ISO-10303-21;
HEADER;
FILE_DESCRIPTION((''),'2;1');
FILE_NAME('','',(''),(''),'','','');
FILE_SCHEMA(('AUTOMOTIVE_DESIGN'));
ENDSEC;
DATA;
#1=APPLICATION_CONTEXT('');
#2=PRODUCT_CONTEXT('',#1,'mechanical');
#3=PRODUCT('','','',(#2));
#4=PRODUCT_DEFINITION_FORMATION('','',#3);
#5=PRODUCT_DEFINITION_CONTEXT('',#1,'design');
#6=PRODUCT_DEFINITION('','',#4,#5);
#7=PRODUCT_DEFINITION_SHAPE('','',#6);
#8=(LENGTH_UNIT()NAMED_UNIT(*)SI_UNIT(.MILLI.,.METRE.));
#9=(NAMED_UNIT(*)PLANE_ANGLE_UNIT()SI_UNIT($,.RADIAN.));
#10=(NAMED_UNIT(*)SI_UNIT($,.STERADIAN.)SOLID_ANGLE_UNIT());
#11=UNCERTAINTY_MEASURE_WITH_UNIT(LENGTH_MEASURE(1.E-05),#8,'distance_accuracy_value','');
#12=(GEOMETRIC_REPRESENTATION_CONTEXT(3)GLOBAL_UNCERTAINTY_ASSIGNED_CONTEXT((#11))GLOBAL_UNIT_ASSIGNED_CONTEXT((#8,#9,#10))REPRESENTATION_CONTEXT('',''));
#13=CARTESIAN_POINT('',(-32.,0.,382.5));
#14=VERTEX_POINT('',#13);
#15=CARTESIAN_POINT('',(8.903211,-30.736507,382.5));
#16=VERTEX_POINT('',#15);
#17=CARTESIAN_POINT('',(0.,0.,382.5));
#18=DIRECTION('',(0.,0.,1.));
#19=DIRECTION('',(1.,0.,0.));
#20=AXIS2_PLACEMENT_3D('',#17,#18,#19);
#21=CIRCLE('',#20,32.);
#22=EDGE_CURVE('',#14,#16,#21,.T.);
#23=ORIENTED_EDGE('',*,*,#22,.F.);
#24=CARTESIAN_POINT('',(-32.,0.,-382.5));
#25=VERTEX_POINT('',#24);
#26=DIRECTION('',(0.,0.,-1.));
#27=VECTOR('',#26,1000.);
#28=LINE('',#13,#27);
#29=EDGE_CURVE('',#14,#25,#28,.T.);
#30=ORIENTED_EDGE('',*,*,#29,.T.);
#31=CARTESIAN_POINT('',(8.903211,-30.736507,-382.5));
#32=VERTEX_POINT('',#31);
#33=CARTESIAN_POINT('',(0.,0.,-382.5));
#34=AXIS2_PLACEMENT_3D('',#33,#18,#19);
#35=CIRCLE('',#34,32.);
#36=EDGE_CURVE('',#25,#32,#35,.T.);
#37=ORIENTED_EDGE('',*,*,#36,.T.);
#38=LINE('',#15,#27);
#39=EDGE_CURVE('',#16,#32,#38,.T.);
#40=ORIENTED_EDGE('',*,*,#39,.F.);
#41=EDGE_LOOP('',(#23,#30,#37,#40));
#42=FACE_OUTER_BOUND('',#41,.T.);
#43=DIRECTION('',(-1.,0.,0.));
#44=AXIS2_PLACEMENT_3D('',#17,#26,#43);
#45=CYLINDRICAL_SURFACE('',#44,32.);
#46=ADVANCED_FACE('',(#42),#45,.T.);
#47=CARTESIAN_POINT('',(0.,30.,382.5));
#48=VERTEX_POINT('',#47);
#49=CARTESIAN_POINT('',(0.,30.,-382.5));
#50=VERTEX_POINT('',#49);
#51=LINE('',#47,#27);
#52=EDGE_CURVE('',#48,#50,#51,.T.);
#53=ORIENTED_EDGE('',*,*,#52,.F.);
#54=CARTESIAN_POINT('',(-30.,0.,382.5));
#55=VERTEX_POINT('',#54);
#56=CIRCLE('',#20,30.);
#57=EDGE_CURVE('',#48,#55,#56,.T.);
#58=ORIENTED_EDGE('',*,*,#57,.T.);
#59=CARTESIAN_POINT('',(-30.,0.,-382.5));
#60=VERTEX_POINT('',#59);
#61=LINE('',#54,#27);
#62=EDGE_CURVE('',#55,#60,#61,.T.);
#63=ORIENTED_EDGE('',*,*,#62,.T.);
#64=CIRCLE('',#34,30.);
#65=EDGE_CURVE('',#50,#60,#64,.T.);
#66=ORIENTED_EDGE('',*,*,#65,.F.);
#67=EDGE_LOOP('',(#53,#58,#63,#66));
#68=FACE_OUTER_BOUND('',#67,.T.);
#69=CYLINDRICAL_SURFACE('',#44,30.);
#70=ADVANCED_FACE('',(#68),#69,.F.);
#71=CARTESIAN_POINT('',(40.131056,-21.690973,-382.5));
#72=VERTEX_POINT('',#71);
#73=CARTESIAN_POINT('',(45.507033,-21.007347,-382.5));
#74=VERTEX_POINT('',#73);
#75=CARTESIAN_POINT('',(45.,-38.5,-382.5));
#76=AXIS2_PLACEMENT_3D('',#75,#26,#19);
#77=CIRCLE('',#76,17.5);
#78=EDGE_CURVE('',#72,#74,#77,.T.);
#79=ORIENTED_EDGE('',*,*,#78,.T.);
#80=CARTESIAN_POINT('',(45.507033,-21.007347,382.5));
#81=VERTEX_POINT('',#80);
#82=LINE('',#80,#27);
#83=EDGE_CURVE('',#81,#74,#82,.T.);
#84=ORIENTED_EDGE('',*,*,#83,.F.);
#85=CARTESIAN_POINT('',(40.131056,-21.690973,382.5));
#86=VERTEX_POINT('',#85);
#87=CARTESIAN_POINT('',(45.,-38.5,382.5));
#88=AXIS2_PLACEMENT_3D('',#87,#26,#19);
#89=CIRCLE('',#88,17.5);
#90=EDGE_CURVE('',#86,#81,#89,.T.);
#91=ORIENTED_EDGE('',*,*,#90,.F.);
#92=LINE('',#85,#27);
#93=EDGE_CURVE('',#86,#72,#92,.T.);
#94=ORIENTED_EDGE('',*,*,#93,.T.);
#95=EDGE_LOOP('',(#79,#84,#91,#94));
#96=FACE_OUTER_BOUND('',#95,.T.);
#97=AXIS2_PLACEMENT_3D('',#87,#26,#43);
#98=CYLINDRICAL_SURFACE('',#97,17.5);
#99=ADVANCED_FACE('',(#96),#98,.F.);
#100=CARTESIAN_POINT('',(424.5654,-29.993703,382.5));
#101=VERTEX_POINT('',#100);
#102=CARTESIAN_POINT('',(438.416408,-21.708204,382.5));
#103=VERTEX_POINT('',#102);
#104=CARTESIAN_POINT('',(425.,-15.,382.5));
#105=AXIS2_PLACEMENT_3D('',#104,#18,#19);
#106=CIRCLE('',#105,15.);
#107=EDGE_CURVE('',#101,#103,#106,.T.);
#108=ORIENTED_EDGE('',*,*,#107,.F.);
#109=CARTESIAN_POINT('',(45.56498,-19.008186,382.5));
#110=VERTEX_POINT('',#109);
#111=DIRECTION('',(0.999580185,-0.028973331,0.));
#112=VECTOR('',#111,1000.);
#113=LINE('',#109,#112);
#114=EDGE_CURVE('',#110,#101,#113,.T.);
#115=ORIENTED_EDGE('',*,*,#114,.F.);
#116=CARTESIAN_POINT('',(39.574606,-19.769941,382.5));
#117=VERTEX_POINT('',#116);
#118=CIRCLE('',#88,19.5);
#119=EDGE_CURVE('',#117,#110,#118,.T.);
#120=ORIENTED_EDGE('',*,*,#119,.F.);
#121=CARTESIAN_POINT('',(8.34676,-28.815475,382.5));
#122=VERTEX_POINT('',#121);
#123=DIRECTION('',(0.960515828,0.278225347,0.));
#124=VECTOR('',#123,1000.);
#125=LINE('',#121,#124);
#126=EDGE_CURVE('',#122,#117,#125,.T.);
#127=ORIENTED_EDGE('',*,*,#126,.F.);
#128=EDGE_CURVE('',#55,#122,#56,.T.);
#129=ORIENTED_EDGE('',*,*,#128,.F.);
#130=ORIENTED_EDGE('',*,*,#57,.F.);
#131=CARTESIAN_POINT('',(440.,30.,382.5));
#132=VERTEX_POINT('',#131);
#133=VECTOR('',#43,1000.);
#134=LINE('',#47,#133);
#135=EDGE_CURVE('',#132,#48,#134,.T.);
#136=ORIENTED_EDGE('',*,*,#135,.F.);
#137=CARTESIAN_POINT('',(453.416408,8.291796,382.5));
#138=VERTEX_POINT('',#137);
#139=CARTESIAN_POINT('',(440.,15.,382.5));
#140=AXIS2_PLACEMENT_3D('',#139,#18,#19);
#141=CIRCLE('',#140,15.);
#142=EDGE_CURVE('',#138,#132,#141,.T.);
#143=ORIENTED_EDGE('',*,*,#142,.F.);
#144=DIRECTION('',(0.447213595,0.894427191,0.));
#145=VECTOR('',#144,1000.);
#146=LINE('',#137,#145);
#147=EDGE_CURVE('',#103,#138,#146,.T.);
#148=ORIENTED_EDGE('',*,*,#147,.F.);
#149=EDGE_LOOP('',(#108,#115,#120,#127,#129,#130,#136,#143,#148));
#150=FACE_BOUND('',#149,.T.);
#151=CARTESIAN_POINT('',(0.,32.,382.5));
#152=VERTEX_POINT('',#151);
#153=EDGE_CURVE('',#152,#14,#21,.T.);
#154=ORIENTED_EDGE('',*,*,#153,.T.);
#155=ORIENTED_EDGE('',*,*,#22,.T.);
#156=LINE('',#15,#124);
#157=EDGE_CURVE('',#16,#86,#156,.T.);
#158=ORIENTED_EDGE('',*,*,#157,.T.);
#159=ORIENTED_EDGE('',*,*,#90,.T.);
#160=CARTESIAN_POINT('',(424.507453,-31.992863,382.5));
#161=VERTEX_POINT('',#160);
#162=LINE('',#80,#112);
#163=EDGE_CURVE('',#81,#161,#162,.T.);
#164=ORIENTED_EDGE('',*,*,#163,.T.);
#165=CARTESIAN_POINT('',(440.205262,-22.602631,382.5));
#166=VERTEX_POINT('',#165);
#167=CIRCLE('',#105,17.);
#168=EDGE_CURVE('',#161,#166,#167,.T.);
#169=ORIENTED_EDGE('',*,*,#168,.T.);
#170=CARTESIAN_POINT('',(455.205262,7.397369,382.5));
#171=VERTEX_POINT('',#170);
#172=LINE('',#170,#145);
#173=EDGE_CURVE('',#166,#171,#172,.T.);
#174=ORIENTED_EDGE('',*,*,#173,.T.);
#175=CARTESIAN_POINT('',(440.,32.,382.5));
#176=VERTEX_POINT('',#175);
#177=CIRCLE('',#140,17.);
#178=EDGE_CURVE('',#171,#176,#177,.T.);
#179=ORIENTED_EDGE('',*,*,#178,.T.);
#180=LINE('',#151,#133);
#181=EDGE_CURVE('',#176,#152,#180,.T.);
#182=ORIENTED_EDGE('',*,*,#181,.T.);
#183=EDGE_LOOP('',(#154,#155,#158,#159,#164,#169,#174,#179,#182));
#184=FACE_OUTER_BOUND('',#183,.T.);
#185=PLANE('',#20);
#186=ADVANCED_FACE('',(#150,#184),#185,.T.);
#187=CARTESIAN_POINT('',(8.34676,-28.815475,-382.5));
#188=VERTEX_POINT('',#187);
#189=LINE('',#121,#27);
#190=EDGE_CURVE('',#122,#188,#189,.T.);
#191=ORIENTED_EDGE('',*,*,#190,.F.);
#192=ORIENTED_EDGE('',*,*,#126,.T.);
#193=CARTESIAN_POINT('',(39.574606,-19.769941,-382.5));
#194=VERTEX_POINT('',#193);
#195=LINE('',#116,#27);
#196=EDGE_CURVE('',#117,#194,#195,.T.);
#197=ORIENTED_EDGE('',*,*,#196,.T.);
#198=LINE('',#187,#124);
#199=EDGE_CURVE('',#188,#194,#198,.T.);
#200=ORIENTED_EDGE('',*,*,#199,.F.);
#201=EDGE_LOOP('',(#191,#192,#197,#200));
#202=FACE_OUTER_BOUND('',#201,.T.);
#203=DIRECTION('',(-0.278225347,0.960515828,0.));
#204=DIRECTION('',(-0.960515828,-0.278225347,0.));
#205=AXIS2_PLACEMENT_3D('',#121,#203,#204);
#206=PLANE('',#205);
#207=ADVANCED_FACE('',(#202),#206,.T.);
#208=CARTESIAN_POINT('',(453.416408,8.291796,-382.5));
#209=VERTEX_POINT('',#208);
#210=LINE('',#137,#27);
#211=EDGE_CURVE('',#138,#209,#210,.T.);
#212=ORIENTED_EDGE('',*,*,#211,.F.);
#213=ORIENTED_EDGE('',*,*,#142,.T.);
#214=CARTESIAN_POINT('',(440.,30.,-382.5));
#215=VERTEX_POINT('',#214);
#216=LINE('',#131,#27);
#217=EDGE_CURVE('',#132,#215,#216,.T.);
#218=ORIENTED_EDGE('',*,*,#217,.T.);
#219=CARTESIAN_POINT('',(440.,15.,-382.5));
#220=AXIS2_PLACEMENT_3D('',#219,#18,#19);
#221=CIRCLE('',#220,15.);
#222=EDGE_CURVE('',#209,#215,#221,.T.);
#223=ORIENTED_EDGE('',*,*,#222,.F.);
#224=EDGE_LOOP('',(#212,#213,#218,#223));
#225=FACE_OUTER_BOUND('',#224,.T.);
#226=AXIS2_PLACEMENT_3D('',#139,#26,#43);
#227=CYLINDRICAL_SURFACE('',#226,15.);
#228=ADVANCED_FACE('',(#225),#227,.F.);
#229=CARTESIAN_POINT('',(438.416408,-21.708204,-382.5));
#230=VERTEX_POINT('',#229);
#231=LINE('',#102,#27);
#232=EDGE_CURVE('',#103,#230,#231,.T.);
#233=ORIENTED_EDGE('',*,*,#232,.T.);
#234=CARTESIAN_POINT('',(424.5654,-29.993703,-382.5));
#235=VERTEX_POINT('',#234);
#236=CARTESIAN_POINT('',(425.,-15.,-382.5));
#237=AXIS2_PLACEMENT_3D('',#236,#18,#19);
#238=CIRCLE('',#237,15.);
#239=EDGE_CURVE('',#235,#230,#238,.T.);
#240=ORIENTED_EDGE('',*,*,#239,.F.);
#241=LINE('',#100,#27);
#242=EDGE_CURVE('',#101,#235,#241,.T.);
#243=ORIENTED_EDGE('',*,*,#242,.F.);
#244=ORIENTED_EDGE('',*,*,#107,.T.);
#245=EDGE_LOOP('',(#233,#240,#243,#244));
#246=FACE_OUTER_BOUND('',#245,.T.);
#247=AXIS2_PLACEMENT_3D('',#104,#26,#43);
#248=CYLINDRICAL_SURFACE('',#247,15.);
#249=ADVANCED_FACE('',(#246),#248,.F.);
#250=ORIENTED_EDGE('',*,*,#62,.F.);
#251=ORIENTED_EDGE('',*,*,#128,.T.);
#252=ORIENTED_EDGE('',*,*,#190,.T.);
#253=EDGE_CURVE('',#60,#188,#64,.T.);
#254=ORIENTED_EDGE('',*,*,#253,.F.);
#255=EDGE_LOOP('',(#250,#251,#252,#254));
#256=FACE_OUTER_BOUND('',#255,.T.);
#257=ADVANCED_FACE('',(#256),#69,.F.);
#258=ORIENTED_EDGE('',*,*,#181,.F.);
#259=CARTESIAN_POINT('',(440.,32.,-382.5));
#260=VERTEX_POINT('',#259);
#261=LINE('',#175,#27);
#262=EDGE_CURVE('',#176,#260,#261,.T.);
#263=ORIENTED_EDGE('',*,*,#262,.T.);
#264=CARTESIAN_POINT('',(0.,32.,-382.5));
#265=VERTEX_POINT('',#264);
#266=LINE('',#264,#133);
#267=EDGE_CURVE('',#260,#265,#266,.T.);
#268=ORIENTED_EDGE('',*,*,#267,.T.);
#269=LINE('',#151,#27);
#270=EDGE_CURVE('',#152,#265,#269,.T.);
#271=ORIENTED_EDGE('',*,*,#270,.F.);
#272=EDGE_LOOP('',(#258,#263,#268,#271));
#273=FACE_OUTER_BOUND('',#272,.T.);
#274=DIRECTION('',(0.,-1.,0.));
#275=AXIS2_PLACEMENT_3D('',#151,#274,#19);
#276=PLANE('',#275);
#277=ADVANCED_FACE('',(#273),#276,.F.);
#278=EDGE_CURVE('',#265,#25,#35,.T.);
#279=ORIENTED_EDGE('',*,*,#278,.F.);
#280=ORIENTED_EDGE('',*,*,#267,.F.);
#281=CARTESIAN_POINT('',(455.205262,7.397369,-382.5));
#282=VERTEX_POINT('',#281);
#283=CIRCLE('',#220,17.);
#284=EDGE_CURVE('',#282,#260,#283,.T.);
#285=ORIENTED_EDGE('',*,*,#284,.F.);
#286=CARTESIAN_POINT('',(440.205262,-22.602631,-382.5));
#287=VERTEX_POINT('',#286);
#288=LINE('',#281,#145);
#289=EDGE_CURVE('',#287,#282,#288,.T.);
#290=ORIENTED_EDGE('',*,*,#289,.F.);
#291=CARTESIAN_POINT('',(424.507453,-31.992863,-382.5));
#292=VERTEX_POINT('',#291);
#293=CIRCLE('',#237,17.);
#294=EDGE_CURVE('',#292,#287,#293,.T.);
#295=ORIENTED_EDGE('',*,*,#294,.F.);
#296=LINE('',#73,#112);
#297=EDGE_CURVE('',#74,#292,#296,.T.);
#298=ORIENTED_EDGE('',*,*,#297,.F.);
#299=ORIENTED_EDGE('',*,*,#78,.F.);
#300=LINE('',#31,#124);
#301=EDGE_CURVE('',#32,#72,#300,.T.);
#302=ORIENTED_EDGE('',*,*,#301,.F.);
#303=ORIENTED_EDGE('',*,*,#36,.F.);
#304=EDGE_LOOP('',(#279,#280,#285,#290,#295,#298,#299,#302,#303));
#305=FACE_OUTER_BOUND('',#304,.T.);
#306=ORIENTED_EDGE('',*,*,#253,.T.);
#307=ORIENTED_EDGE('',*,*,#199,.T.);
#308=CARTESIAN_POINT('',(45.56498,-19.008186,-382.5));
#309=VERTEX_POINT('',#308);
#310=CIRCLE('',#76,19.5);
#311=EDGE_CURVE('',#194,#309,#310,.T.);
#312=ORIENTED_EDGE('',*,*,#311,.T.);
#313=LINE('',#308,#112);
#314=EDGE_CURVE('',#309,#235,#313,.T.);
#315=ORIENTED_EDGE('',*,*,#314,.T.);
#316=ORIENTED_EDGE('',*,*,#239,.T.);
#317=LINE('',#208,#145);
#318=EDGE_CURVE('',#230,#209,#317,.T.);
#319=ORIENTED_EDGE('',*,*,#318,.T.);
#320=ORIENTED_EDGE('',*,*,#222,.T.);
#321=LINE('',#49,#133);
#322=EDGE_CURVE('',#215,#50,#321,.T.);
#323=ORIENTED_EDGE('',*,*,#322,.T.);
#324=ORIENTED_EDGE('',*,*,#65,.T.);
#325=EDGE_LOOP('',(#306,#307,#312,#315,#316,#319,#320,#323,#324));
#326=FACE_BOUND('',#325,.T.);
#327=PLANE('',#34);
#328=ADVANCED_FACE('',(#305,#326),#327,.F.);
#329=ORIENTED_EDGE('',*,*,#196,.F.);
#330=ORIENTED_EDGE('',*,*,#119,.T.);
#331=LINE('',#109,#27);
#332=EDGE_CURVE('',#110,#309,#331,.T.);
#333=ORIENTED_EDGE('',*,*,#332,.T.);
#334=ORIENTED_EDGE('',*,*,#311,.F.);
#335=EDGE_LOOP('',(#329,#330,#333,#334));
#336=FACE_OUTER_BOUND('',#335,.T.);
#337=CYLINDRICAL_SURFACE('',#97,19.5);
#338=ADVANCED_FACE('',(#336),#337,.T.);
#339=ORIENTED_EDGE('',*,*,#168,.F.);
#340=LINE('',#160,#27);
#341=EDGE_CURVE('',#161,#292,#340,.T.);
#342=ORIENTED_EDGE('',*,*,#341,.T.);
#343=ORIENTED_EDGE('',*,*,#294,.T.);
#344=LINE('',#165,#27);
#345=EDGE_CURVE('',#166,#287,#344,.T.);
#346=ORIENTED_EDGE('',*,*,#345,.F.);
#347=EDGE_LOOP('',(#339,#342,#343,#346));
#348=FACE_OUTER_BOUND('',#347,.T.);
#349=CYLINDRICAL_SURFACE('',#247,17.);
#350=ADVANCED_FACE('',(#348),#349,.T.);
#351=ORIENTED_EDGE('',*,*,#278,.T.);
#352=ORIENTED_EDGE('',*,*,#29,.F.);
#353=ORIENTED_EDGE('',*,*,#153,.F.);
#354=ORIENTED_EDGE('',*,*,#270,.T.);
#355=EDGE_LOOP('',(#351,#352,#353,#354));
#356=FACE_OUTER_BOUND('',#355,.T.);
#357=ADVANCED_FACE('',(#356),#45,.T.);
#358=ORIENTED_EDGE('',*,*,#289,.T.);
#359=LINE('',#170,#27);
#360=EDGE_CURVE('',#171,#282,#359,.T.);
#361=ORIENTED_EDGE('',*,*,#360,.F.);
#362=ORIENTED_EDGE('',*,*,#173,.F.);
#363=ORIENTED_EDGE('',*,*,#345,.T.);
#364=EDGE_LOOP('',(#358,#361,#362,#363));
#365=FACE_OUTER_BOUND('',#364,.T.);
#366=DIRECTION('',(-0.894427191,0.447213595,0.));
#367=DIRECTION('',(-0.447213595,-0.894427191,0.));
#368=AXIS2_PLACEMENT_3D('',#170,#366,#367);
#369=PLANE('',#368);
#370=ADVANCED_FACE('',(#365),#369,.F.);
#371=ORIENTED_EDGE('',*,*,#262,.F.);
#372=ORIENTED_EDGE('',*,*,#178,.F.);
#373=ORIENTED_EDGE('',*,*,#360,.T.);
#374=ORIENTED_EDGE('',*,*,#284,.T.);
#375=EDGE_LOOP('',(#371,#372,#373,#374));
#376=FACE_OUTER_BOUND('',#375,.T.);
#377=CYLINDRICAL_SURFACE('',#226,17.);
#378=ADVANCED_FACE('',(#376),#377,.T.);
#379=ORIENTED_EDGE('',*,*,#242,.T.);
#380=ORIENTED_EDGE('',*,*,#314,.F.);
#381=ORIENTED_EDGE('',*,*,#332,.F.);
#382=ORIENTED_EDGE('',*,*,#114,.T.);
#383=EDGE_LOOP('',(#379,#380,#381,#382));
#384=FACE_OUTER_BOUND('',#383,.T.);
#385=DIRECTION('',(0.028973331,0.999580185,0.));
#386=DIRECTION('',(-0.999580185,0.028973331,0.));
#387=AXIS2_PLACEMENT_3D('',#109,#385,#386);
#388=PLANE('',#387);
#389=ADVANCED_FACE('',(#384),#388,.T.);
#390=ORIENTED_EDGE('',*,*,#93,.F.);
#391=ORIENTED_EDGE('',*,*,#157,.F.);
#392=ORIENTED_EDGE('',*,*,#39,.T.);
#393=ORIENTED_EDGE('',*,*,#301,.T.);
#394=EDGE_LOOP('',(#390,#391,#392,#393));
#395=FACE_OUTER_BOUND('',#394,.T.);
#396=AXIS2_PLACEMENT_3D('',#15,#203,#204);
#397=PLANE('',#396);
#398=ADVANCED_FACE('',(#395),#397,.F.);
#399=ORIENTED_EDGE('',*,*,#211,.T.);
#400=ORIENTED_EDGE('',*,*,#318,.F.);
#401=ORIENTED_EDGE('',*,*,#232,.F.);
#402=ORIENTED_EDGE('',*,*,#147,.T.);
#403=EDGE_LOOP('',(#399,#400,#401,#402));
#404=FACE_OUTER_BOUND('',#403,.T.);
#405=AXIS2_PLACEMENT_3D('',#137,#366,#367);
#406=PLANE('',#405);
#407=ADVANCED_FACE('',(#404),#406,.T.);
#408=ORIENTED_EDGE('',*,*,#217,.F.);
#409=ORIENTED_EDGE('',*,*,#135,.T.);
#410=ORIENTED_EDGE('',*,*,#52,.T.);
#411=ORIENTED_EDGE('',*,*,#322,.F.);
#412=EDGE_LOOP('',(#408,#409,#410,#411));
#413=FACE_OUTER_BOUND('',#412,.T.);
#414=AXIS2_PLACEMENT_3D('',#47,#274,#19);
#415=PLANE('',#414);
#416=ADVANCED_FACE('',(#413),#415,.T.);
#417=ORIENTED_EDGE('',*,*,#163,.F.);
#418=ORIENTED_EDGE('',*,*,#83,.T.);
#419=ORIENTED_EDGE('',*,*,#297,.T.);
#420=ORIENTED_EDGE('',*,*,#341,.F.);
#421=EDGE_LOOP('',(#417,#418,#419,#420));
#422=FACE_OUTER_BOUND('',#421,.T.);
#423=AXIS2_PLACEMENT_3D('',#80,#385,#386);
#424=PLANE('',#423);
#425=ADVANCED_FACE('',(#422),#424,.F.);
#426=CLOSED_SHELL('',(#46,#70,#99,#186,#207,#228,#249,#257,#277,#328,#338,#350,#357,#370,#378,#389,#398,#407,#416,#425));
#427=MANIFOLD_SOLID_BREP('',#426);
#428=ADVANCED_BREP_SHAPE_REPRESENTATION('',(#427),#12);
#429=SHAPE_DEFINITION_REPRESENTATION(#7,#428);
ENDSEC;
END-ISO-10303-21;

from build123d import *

# Parameters (mm, degrees)
EXTRUDE_1_DEPTH = 382.5


with BuildPart() as part:
    # 草图1 → 凸台-拉伸1 (new, symmetric)
    with BuildSketch(Plane.XY):
        with BuildLine():
            Line((8.903211102, -30.736506504), (40.131056429, -21.690973006))
            ThreePointArc((40.131056429, -21.690973006), (42.792421792, -21.139798433), (45.507033287, -21.007346764))
            Line((45.507033287, -21.007346764), (424.507453379, -31.992863144))
            ThreePointArc((424.507453379, -31.992863144), (433.726976259, -29.589033052), (440.205262247, -22.602631123))
            Line((440.205262247, -22.602631123), (455.205262247, 7.397368877))
            ThreePointArc((455.205262247, 7.397368877), (454.461063742, 23.937428906), (440, 32))
            Line((440, 32), (0, 32))
            ThreePointArc((0, 32), (-31.682552045, -4.496209063), (8.903211102, -30.736506504))
        make_face()
        with BuildLine():
            Line((0, 30), (440, 30))
            ThreePointArc((440, 30), (452.759762125, 22.885966682), (453.416407865, 8.291796068))
            Line((453.416407865, 8.291796068), (438.416407865, -21.708203932))
            ThreePointArc((438.416407865, -21.708203932), (432.700273169, -27.872676222), (424.56540004, -29.993702774))
            Line((424.56540004, -29.993702774), (45.564979948, -19.008186394))
            ThreePointArc((45.564979948, -19.008186394), (42.54012714, -19.155775396), (39.574605735, -19.769941349))
            Line((39.574605735, -19.769941349), (8.346760408, -28.815474848))
            ThreePointArc((8.346760408, -28.815474848), (-29.702392542, -4.215195996), (0, 30))
        make_face(mode=Mode.SUBTRACT)
    extrude(amount=EXTRUDE_1_DEPTH, both=True)


solid = part.part
